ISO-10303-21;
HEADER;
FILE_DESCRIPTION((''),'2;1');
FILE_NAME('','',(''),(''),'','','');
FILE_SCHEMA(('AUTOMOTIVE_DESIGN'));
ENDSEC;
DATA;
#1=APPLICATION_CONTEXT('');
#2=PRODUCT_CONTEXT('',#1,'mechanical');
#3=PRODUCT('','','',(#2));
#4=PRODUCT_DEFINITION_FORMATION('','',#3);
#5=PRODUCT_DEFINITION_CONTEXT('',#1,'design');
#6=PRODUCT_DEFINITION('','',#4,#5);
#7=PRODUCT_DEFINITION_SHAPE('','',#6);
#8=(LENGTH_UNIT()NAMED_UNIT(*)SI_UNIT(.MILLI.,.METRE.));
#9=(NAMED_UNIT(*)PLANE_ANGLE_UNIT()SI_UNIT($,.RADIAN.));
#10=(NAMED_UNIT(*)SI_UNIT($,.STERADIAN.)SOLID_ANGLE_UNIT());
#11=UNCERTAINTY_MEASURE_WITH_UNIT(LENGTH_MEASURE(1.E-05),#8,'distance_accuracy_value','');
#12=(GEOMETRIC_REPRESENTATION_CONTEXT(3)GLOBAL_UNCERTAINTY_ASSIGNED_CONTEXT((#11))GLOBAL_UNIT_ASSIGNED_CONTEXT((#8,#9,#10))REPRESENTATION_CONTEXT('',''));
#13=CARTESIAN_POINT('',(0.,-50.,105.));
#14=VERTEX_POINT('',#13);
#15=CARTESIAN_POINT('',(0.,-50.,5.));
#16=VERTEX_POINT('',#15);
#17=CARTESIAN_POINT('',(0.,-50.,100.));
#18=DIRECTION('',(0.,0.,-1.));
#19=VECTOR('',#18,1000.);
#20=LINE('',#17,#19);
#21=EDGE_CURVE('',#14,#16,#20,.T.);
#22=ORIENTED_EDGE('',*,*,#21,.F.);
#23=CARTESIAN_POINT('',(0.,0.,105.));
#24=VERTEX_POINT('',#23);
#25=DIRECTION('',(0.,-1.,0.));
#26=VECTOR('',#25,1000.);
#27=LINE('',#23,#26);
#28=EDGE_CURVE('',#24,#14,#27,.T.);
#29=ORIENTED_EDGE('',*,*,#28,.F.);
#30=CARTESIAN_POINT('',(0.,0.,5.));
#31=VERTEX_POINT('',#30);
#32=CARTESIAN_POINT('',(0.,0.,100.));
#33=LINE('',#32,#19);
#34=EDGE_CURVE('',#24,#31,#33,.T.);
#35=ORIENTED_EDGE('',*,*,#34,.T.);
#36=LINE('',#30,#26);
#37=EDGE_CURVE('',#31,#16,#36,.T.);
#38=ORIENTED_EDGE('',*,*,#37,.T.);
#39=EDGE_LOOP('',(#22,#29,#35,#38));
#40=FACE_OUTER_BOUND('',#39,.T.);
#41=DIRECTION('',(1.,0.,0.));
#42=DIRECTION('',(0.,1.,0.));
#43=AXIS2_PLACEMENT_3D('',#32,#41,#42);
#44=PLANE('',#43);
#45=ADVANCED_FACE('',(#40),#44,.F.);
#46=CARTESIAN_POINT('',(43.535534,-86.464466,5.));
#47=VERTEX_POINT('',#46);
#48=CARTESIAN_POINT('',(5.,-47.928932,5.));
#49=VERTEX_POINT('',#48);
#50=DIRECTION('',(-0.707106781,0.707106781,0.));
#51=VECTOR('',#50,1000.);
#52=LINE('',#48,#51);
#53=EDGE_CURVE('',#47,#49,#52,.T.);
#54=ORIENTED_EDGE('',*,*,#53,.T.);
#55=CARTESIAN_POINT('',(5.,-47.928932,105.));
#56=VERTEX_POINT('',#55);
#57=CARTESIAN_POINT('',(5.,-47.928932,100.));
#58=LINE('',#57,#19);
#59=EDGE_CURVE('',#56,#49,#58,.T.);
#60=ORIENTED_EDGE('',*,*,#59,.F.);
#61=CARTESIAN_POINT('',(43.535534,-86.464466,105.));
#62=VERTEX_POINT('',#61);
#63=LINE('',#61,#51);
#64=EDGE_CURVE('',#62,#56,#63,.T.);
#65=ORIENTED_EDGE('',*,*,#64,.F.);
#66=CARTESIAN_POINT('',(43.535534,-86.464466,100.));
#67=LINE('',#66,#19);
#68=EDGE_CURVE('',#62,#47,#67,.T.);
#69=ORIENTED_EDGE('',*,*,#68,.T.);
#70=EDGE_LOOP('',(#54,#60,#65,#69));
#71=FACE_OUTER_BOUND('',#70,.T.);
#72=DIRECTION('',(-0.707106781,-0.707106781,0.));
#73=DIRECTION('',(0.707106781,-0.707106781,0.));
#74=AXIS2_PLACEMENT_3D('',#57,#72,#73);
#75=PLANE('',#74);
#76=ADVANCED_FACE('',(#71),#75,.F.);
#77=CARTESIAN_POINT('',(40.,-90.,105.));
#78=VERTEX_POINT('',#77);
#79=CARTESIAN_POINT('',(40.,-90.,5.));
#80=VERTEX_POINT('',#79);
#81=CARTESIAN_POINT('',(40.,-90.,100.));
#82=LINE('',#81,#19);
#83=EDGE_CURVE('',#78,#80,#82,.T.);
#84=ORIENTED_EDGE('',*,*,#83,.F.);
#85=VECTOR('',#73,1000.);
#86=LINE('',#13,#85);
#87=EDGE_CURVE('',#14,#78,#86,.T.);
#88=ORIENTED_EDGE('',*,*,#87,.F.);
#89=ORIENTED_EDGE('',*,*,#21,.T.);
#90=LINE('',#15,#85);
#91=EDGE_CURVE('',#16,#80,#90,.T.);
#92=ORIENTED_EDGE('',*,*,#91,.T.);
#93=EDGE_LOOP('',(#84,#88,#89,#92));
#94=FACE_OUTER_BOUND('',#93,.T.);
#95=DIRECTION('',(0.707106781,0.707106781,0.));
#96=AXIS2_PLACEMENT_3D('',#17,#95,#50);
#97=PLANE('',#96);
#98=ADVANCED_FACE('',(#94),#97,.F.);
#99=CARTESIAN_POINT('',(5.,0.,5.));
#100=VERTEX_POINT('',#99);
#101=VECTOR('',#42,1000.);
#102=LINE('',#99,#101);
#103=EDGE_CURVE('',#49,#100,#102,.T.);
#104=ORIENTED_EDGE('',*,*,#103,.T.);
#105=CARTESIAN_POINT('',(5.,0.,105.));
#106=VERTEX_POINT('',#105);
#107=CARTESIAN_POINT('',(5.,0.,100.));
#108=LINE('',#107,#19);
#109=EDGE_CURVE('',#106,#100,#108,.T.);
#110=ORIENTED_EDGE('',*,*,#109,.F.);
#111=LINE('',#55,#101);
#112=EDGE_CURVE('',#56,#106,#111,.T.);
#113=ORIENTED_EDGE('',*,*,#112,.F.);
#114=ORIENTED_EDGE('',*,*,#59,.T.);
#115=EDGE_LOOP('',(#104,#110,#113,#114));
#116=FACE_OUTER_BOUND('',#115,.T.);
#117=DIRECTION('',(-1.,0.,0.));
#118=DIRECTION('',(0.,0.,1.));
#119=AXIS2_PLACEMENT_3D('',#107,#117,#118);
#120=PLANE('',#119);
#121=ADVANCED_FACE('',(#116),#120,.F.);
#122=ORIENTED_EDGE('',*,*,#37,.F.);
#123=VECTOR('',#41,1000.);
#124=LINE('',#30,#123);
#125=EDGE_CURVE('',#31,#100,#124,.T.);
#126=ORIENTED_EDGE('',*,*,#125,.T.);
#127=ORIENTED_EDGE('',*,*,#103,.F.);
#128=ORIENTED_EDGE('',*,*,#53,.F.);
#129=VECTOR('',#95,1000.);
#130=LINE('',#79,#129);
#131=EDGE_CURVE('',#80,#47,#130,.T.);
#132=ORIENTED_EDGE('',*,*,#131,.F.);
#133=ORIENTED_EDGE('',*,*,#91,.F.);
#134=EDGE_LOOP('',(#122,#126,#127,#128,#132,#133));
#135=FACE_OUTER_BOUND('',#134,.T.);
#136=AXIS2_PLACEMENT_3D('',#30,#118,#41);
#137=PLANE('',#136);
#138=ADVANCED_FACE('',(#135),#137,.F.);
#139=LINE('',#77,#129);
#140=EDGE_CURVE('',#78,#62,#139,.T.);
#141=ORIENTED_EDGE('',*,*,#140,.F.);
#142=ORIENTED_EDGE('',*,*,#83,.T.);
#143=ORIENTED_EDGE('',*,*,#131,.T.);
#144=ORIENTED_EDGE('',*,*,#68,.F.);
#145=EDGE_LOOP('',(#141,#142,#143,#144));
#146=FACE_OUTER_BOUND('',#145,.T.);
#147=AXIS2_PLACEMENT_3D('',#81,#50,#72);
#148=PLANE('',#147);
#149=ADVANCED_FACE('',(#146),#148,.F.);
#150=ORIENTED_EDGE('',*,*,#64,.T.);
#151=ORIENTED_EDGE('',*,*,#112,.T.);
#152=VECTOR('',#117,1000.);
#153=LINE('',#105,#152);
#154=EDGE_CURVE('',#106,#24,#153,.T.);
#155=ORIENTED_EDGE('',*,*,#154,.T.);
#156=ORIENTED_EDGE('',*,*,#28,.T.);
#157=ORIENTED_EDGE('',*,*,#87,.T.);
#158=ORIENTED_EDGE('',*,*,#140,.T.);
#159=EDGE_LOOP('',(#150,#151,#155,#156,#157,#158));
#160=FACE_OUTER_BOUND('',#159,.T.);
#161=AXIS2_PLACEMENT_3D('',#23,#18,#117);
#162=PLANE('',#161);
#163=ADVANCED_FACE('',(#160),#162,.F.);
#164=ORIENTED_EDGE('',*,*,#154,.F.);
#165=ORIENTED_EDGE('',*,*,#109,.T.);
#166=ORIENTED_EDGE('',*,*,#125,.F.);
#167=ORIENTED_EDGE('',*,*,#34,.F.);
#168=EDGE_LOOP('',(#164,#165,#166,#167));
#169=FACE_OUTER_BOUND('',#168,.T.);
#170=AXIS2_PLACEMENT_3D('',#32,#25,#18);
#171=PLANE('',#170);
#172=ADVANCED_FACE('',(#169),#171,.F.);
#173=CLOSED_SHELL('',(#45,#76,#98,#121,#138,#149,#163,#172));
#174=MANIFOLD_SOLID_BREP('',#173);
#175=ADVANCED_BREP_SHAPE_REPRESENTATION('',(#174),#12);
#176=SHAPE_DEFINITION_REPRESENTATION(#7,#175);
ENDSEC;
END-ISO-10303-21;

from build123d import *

# Parameters (mm, degrees)
EXTRUDE_2_DEPTH          = 100
CUT_EXTRUDE_1_DEPTH      = 140.946373206
CUT_EXTRUDE_1_DEPTH_BACK = 140.946373206
SKETCH_2_W               = 5
SKETCH_2_H               = 42.071067812
EXTRUDE_3_DEPTH          = 10


with BuildPart() as part:
    # 草图1 → 凸台-拉伸2 (new body)
    with BuildSketch(Plane.XY):
        Polygon((0, 0), (0, -50), (40, -90), (43.535533906, -86.464466094), (5, -47.928932188), (5, 0), align=None)
    extrude(amount=EXTRUDE_2_DEPTH)

    # 草图2 → 切除-拉伸1 (cut, two sides: drawn at the far end of the back side and taken through both)
    with BuildSketch(Plane(origin=(5, 0, 0), x_dir=(0, 0, -1), z_dir=(1, 0, 0)).offset(-CUT_EXTRUDE_1_DEPTH_BACK)):
        Polygon((0, 0), (-5, 0), (-5, -5), (-5, -42.928932188), (-5, -47.928932188), (0, -47.928932188), align=None)
        with Locations((-2.5, -68.964466094)):
            Rectangle(SKETCH_2_W, SKETCH_2_H)
        with Locations((-97.5, -68.964466094)):
            Rectangle(SKETCH_2_W, SKETCH_2_H)
        Polygon((-95, -5), (-95, 0), (-100, 0), (-100, -47.928932188), (-95, -47.928932188), (-95, -42.928932188), align=None)
    extrude(amount=CUT_EXTRUDE_1_DEPTH + CUT_EXTRUDE_1_DEPTH_BACK, mode=Mode.SUBTRACT)

    # 草图3 → 凸台-拉伸3 (add)
    with BuildSketch(Plane.XY.offset(95)):
        Polygon((0, -50), (40, -90), (43.535533906, -86.464466094), (5, -47.928932188), (5, 0), (0, 0), align=None)
    extrude(amount=EXTRUDE_3_DEPTH)


solid = part.part
